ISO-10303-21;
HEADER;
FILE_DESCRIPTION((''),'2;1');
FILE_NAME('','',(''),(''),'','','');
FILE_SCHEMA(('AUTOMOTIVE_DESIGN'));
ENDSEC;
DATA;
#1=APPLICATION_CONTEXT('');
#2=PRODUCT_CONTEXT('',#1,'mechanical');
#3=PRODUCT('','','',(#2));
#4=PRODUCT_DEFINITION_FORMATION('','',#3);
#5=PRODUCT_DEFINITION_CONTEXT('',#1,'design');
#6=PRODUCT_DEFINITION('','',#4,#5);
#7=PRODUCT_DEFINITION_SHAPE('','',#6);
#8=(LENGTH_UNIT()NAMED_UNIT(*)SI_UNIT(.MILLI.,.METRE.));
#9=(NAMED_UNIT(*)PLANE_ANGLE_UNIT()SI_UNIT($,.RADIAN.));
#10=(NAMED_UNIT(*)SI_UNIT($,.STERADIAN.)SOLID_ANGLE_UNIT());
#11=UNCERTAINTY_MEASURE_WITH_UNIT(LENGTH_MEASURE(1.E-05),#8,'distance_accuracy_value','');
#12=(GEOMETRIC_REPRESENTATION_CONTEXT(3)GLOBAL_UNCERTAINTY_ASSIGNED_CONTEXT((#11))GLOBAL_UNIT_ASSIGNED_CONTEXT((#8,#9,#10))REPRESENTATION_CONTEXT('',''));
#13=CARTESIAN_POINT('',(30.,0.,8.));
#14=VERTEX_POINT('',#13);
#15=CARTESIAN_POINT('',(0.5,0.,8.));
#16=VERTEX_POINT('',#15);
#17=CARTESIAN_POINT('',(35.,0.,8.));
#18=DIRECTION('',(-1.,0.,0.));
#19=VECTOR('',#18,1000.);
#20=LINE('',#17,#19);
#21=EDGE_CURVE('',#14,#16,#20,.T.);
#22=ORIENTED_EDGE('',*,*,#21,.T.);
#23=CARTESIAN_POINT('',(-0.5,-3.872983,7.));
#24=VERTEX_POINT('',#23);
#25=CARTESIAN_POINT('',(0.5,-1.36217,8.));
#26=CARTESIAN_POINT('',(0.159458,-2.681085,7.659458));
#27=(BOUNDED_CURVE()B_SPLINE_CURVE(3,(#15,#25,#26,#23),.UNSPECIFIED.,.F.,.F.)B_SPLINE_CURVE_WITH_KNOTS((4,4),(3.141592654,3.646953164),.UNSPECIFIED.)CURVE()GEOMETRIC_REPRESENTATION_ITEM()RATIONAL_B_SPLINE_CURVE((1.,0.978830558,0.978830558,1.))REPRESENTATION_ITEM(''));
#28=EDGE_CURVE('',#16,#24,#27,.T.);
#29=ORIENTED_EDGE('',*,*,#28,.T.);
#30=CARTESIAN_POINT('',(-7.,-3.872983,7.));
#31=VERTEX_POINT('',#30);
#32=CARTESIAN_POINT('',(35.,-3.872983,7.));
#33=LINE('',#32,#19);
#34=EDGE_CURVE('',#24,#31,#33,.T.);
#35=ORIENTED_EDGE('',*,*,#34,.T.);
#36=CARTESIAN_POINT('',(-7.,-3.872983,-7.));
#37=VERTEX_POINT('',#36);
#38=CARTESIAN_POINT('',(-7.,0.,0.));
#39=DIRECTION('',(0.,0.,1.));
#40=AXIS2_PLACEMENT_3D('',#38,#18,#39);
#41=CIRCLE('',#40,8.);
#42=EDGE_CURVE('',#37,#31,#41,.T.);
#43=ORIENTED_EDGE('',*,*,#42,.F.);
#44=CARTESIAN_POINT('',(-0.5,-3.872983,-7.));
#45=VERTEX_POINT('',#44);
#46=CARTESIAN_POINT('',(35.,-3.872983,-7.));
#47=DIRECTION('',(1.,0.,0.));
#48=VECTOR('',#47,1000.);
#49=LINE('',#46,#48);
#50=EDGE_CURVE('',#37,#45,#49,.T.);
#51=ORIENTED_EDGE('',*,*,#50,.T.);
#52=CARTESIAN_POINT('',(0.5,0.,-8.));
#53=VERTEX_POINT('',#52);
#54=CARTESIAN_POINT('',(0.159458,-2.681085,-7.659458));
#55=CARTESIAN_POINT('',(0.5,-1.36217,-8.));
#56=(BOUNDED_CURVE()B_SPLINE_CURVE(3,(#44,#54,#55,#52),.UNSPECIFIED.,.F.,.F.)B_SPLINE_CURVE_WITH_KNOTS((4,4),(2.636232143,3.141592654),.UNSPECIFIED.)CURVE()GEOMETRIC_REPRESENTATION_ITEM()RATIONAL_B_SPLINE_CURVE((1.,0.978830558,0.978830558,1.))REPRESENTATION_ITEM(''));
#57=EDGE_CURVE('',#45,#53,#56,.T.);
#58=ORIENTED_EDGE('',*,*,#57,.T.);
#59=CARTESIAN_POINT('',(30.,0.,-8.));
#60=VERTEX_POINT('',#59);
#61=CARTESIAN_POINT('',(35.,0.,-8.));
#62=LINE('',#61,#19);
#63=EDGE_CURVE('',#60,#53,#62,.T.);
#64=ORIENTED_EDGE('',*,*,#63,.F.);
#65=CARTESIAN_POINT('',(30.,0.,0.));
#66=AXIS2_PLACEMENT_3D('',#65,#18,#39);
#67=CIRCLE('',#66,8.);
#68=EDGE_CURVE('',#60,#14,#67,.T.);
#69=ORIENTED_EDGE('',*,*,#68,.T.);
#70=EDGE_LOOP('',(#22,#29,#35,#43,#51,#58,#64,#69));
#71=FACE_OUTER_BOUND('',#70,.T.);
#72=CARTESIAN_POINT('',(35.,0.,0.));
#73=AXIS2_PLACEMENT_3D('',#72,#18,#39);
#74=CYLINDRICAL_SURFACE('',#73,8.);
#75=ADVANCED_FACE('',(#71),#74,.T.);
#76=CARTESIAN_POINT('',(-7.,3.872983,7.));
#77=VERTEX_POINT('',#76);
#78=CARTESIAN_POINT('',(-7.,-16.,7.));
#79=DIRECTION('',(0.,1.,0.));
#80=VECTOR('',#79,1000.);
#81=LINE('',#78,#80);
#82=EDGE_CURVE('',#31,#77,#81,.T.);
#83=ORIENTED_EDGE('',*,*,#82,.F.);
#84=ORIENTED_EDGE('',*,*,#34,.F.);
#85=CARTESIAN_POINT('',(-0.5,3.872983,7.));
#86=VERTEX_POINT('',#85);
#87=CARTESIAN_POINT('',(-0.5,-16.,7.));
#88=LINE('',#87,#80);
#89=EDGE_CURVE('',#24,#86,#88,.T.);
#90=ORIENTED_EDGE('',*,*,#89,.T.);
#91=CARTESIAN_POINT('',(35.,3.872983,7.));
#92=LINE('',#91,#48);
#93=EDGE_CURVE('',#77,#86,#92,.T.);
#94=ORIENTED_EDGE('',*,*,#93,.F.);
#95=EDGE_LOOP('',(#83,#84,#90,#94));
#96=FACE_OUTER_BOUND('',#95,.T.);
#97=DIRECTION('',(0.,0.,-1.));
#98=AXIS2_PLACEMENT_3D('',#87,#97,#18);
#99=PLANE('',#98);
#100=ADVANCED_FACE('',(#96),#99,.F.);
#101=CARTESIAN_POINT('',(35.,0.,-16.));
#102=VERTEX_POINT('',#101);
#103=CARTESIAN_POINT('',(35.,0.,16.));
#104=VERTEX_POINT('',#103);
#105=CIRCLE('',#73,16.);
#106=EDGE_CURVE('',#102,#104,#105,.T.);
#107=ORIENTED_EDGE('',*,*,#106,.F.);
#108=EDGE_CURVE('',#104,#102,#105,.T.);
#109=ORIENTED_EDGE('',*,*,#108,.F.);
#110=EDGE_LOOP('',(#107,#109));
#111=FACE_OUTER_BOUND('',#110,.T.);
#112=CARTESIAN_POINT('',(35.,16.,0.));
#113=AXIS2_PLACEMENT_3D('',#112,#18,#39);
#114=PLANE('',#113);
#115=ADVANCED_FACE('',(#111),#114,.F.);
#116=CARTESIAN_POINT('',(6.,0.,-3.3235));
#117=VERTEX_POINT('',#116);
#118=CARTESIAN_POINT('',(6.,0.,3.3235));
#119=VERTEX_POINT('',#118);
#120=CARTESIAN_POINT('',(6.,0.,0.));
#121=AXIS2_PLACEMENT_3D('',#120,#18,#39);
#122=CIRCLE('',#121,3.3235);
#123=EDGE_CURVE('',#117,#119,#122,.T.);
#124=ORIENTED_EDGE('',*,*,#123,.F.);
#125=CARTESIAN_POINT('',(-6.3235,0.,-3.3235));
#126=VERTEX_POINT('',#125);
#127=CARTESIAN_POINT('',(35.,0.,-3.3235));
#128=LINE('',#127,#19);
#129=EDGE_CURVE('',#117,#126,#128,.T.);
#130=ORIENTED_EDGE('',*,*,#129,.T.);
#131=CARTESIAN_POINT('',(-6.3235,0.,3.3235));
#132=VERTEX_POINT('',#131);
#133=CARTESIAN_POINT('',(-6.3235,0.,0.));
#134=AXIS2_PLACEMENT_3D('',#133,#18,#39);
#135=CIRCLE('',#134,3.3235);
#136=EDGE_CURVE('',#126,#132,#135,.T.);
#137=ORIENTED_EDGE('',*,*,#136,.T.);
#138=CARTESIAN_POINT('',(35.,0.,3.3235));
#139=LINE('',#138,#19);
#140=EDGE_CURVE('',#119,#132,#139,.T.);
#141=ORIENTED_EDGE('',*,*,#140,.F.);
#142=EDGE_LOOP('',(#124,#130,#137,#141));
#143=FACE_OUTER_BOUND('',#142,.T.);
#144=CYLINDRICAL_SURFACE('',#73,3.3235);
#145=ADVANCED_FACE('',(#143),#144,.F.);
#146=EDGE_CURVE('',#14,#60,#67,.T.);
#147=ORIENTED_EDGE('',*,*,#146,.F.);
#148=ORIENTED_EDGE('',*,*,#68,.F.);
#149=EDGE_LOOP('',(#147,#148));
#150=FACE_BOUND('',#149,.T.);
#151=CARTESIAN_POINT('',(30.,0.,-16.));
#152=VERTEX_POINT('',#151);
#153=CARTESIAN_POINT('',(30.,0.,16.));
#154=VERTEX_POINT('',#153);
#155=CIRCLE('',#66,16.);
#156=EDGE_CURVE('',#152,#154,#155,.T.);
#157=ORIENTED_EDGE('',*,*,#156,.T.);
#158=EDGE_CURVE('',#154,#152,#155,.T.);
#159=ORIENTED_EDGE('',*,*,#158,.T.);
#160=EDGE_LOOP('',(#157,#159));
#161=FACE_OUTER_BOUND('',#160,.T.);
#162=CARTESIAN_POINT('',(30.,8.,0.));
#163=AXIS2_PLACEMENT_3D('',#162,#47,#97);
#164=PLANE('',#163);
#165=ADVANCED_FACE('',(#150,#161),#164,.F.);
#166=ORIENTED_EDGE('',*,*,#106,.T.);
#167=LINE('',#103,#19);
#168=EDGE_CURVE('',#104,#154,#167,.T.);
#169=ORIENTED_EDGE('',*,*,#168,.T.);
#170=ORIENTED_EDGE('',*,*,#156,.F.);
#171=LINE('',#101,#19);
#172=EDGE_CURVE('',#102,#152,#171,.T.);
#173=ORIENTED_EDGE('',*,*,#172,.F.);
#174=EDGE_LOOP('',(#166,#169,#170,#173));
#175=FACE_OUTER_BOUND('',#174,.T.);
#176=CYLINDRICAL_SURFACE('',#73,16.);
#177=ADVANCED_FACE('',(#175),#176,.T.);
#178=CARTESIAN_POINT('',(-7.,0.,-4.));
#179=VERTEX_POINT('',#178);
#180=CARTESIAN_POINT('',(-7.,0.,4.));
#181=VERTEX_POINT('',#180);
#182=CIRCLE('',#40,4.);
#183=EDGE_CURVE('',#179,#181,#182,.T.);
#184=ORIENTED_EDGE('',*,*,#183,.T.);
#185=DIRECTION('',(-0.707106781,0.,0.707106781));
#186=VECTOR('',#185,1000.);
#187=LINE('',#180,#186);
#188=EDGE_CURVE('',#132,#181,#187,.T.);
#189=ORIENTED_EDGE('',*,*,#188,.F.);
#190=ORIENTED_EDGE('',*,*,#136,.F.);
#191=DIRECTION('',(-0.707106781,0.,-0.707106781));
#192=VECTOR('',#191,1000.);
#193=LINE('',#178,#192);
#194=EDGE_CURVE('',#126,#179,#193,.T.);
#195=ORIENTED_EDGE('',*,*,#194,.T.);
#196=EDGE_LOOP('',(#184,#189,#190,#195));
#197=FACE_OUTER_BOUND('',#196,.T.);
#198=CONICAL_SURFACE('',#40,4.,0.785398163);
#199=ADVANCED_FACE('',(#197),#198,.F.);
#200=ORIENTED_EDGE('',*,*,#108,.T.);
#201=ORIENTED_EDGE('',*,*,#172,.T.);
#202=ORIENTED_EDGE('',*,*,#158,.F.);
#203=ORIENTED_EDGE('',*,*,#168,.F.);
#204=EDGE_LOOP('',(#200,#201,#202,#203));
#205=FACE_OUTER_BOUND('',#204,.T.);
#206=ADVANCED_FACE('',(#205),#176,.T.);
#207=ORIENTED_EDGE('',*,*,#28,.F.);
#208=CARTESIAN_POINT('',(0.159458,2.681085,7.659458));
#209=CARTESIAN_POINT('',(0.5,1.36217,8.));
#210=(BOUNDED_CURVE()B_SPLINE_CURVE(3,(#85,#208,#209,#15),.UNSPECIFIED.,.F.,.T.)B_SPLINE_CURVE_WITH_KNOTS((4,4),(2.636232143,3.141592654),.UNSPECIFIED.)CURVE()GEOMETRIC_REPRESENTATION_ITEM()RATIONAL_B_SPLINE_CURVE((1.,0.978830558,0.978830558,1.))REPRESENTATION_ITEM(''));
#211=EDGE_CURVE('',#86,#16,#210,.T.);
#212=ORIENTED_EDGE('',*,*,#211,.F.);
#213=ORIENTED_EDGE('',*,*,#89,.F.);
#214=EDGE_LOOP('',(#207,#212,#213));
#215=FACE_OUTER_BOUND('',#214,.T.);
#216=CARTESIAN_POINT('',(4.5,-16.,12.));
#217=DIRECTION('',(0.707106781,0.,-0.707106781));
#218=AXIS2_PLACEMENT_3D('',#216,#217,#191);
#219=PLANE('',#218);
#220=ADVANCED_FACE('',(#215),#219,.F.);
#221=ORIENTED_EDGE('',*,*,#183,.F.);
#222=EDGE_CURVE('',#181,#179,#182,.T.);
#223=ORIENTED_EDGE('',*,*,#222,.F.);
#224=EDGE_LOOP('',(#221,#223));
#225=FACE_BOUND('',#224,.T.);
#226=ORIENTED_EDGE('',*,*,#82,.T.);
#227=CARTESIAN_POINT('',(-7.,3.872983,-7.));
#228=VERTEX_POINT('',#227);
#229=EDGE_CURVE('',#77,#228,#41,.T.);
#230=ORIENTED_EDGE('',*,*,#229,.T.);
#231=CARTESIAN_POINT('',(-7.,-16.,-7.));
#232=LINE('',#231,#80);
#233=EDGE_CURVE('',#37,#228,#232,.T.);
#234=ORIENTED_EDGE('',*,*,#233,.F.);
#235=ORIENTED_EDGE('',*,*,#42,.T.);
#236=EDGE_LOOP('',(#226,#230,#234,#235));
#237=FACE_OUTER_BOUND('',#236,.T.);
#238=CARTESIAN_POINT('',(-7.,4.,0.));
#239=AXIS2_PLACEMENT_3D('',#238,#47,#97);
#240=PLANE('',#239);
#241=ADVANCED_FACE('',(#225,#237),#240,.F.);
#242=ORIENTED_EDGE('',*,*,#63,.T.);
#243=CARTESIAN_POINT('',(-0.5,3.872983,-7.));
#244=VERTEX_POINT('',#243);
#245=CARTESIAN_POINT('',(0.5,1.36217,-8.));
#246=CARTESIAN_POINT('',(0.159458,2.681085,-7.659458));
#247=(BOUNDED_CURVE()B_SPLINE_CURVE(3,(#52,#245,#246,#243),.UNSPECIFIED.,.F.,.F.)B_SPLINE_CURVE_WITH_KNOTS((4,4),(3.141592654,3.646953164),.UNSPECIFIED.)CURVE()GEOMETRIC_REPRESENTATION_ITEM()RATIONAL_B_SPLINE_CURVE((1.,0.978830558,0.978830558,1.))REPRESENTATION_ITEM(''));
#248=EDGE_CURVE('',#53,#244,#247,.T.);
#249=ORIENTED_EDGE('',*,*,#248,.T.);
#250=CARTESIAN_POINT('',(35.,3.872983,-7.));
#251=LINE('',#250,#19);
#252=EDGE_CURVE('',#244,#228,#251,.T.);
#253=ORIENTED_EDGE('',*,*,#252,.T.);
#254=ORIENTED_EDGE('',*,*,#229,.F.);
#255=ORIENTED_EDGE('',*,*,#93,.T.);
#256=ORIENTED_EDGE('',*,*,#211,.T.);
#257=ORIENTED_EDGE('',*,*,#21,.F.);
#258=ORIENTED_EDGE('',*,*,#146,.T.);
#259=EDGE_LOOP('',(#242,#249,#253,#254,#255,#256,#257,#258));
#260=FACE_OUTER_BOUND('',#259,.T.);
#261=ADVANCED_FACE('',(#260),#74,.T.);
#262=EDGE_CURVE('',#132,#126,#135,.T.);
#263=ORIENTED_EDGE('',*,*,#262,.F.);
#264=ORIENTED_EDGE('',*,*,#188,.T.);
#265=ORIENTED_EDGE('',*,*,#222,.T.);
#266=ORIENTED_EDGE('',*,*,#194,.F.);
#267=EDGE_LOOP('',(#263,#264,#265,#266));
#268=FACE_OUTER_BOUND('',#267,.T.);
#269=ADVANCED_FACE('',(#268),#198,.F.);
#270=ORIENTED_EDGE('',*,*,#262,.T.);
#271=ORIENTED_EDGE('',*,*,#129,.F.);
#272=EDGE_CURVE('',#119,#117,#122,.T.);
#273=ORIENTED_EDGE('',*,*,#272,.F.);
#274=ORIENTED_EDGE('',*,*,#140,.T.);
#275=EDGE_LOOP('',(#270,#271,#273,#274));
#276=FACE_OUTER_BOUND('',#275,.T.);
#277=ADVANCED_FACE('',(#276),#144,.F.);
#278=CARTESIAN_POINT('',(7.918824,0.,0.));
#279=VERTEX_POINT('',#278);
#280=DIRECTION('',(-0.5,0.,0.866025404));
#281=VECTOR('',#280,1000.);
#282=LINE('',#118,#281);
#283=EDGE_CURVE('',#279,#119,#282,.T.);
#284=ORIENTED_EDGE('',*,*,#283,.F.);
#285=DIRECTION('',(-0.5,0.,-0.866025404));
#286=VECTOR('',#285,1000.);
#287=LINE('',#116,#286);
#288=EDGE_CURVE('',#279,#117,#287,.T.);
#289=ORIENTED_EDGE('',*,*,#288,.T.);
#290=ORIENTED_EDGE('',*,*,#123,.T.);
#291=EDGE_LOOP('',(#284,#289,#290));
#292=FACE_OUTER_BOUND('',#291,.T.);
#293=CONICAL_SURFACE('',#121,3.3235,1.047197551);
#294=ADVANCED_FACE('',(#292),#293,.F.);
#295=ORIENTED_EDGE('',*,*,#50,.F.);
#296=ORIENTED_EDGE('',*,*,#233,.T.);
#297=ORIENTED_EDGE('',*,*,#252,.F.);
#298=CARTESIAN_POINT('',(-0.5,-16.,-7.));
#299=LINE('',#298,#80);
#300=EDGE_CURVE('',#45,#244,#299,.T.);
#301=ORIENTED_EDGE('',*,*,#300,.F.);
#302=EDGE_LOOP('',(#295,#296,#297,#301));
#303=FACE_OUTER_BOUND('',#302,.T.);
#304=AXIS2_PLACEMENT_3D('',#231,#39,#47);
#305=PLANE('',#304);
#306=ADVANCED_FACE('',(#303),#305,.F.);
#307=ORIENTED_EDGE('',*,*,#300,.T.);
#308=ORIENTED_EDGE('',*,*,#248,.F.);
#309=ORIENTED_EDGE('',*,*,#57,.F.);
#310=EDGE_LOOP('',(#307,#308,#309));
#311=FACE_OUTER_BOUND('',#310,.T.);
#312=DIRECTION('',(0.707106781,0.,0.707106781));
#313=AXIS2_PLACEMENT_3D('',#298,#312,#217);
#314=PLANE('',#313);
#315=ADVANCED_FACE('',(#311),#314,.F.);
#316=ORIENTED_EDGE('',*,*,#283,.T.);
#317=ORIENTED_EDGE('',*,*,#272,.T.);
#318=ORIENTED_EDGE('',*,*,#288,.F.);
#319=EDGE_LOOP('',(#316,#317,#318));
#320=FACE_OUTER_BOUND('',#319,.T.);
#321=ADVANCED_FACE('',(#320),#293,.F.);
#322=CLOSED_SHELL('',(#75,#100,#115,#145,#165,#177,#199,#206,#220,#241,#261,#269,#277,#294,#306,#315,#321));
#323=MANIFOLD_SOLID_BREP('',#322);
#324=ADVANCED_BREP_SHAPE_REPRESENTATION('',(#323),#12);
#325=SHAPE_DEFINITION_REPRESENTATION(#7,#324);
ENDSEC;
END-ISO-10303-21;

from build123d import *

# Parameters (mm, degrees)
CUT_EXTRUDE1_DEPTH      = 16
CUT_EXTRUDE1_DEPTH_BACK = 16


with BuildPart() as part:
    # Sketch1 → Revolve1 (revolve)
    with BuildSketch(Plane.XY, mode=Mode.PRIVATE) as revolve1_sk:
        Polygon((7.91882362, 0), (6, 3.3235), (-6.3235, 3.3235), (-7, 4), (-7, 8), (30, 8), (30, 16), (35, 16), (35, 0), align=None)
    revolve(revolve1_sk.sketch.rotate(Axis((35, 0, 0), (-1, 0, 0)), 270), axis=Axis((35, 0, 0), (-1, 0, 0)))

    # Sketch2 → Cut-Extrude1 (cut, two sides: drawn at the far end of the back side and taken through both)
    with BuildSketch(Plane(origin=(0, 0, 0), x_dir=(1, 0, 0), z_dir=(0, 1, 0)).offset(-CUT_EXTRUDE1_DEPTH_BACK)):
        Polygon((-12, 12), (-12, -12), (4.5, -12), (-0.5, -7), (-7, -7), (-7, 7), (-0.5, 7), (4.5, 12), align=None)
    extrude(amount=CUT_EXTRUDE1_DEPTH + CUT_EXTRUDE1_DEPTH_BACK, mode=Mode.SUBTRACT)


solid = part.part
